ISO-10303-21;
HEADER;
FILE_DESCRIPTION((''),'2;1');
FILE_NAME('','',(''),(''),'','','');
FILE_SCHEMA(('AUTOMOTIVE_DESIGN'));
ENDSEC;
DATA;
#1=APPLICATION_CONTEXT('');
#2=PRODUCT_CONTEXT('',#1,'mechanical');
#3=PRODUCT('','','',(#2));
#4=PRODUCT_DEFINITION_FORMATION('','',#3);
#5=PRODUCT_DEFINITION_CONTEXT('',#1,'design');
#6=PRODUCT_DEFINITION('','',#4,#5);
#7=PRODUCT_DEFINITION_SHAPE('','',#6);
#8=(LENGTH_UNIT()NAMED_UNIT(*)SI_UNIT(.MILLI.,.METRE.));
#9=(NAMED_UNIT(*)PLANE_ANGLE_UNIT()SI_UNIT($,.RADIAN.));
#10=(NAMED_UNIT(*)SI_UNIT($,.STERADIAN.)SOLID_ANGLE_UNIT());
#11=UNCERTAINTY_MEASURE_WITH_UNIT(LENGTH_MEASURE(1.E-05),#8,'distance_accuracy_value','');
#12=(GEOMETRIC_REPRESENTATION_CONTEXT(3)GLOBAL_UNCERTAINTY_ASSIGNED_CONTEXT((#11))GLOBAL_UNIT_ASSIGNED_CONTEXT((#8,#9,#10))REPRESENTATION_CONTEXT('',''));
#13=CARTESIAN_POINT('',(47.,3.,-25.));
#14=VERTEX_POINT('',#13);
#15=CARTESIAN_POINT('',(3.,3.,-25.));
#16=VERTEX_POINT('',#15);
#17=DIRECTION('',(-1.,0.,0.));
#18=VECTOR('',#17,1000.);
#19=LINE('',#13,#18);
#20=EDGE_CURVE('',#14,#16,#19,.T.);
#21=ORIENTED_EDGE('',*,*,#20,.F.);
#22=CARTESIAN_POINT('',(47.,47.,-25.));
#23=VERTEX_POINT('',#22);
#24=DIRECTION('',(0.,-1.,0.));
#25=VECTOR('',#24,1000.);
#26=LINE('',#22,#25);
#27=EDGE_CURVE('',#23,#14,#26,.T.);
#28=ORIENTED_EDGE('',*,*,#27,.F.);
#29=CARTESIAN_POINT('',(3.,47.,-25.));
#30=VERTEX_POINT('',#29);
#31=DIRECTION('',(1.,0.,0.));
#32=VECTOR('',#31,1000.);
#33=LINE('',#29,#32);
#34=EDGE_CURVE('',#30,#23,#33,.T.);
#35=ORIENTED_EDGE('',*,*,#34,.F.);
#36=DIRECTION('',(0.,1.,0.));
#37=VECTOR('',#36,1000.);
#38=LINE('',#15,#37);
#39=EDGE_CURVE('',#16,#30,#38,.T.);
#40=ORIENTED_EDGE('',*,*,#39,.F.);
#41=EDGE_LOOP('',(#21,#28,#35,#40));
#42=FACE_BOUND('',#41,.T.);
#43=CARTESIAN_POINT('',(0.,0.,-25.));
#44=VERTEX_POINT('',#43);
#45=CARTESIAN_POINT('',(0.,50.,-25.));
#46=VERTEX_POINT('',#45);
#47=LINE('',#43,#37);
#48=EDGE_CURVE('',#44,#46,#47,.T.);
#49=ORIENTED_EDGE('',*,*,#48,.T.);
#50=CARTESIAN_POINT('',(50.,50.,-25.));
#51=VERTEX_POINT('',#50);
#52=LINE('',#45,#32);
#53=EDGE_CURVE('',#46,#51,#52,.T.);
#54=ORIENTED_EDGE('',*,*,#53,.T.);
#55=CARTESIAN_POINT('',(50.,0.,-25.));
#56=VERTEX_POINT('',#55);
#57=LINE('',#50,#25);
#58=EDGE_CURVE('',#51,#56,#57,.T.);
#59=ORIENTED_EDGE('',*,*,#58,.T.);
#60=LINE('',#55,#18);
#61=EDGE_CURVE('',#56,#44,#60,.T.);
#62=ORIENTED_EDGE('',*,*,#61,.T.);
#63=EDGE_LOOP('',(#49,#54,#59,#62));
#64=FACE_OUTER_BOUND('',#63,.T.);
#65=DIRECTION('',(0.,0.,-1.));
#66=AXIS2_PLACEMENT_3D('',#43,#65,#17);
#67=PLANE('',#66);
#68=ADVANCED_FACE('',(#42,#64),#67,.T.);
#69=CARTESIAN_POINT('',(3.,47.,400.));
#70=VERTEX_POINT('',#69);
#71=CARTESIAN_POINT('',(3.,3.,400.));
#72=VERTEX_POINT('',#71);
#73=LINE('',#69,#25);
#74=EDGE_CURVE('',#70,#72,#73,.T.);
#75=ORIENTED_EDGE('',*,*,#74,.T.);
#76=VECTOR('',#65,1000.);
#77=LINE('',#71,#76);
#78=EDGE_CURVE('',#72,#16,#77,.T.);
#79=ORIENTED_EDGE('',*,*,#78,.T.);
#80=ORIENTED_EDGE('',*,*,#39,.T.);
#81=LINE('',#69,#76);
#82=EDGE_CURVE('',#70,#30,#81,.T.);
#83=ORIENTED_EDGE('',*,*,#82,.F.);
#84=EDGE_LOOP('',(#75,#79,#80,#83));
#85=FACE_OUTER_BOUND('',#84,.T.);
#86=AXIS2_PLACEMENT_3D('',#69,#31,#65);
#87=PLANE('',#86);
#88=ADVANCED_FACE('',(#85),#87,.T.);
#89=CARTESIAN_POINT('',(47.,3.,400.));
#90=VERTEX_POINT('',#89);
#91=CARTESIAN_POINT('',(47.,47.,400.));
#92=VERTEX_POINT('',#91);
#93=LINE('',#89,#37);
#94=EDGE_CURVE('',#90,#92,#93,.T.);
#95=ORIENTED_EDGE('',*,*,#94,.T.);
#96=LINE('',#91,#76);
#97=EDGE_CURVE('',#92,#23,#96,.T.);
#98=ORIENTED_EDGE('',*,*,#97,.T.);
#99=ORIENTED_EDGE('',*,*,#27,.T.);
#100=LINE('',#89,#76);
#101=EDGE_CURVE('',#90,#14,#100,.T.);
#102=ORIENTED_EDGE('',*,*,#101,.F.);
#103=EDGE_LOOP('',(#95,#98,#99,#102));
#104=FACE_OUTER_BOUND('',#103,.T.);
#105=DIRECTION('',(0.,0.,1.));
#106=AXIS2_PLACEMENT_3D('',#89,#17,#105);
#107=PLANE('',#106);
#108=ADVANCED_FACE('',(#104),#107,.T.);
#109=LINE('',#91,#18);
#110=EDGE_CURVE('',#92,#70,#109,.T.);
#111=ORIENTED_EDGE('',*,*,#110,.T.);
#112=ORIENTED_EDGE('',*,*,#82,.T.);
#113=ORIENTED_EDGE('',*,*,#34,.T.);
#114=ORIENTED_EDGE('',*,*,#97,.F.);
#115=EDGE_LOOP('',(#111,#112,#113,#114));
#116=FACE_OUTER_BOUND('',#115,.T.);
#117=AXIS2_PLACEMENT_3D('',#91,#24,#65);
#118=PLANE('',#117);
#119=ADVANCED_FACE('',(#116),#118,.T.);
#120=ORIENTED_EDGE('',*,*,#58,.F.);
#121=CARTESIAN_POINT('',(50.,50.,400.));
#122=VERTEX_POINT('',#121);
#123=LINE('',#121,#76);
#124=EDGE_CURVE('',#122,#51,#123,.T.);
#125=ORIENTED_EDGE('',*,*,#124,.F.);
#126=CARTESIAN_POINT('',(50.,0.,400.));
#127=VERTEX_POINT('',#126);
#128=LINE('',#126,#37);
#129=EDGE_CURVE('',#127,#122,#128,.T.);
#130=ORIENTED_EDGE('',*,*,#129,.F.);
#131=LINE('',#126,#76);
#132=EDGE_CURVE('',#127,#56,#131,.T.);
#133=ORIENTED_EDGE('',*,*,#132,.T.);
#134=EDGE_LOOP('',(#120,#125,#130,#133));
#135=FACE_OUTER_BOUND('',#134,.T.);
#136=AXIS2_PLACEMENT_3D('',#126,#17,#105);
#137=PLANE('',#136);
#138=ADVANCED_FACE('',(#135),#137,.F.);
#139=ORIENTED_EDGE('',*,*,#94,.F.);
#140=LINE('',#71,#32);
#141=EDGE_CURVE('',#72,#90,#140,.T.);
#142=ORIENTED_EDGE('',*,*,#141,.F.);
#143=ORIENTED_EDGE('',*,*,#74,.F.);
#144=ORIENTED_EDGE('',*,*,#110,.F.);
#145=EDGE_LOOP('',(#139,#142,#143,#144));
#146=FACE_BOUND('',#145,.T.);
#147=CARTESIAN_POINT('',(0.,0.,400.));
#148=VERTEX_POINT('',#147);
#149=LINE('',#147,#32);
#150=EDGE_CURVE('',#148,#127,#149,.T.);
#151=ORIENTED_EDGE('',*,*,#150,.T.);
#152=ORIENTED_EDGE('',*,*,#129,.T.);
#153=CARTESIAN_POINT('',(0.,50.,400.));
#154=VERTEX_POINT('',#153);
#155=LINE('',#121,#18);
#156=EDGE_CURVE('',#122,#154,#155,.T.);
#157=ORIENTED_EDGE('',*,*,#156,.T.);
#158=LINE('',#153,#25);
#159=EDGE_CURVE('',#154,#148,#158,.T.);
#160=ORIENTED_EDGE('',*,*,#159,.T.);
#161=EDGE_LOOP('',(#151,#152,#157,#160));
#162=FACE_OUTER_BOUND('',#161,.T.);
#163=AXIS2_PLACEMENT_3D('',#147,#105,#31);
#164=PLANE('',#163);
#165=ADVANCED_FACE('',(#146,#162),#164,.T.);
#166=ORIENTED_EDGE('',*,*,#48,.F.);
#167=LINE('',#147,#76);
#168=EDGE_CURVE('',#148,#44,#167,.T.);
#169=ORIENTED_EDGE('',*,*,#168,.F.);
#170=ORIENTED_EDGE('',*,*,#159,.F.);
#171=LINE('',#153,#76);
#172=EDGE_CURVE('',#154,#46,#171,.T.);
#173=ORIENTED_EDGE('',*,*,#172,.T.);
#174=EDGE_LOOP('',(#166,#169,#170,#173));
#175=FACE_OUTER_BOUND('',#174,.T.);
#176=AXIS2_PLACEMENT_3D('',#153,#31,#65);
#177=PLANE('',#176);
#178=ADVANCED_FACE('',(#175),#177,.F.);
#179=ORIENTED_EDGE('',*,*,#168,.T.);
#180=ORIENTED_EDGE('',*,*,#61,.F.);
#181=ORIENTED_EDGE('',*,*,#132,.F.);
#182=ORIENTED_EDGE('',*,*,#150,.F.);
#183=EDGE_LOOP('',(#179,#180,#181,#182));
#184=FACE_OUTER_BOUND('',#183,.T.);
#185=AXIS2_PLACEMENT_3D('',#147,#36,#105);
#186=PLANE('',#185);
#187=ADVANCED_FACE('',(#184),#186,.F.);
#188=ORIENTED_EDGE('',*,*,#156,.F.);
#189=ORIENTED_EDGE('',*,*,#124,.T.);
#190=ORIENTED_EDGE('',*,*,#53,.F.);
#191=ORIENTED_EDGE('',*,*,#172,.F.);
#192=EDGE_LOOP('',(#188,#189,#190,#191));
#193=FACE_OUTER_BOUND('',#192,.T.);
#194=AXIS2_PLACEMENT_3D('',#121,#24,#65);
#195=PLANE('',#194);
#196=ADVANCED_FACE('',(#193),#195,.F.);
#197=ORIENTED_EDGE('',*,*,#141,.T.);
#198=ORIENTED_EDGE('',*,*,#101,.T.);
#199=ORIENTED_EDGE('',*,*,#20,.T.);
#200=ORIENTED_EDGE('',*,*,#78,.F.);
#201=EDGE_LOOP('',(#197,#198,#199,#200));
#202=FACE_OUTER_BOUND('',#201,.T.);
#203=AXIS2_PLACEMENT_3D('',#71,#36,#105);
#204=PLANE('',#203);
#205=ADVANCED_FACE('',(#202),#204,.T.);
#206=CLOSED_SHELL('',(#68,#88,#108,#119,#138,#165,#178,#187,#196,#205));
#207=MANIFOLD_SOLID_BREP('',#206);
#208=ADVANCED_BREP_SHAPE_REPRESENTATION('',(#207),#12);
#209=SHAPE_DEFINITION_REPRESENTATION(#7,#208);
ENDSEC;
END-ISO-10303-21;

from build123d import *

# Parameters (mm, degrees)
SKETCH_1_W          = 50
SKETCH_1_H          = 50
SKETCH_1_W_2        = 44
SKETCH_1_H_2        = 44
EXTRUDE_1_DEPTH     = 400
SKETCH_2_W          = 50
SKETCH_2_H          = 50
SKETCH_2_W_2        = 44
SKETCH_2_H_2        = 44
CUT_EXTRUDE_1_DEPTH = 25
SKETCH_3_W          = 50
SKETCH_3_H          = 50
SKETCH_3_W_2        = 44
SKETCH_3_H_2        = 44
EXTRUDE_2_DEPTH     = 50


with BuildPart() as part:
    # 草图1 → 凸台-拉伸1 (new body)
    with BuildSketch(Plane.XY):
        with Locations((25, 25)):
            Rectangle(SKETCH_1_W, SKETCH_1_H)
        with Locations((25, 25)):
            Rectangle(SKETCH_1_W_2, SKETCH_1_H_2, mode=Mode.SUBTRACT)
    extrude(amount=EXTRUDE_1_DEPTH)

    # 草图2 → 切除-拉伸1 (cut)
    with BuildSketch(Plane(origin=(0, 0, 0), x_dir=(-1, 0, 0), z_dir=(0, 0, -1))):
        with Locations((-25, 25)):
            Rectangle(SKETCH_2_W, SKETCH_2_H)
        with Locations((-25, 25)):
            Rectangle(SKETCH_2_W_2, SKETCH_2_H_2, mode=Mode.SUBTRACT)
    extrude(amount=-CUT_EXTRUDE_1_DEPTH, mode=Mode.SUBTRACT)

    # 草图3 → 凸台-拉伸2 (add)
    with BuildSketch(Plane(origin=(0, 0, 25), x_dir=(-1, 0, 0), z_dir=(0, 0, -1))):
        with Locations((-25, 25)):
            Rectangle(SKETCH_3_W, SKETCH_3_H)
        with Locations((-25, 25)):
            Rectangle(SKETCH_3_W_2, SKETCH_3_H_2, mode=Mode.SUBTRACT)
    extrude(amount=EXTRUDE_2_DEPTH)


solid = part.part
